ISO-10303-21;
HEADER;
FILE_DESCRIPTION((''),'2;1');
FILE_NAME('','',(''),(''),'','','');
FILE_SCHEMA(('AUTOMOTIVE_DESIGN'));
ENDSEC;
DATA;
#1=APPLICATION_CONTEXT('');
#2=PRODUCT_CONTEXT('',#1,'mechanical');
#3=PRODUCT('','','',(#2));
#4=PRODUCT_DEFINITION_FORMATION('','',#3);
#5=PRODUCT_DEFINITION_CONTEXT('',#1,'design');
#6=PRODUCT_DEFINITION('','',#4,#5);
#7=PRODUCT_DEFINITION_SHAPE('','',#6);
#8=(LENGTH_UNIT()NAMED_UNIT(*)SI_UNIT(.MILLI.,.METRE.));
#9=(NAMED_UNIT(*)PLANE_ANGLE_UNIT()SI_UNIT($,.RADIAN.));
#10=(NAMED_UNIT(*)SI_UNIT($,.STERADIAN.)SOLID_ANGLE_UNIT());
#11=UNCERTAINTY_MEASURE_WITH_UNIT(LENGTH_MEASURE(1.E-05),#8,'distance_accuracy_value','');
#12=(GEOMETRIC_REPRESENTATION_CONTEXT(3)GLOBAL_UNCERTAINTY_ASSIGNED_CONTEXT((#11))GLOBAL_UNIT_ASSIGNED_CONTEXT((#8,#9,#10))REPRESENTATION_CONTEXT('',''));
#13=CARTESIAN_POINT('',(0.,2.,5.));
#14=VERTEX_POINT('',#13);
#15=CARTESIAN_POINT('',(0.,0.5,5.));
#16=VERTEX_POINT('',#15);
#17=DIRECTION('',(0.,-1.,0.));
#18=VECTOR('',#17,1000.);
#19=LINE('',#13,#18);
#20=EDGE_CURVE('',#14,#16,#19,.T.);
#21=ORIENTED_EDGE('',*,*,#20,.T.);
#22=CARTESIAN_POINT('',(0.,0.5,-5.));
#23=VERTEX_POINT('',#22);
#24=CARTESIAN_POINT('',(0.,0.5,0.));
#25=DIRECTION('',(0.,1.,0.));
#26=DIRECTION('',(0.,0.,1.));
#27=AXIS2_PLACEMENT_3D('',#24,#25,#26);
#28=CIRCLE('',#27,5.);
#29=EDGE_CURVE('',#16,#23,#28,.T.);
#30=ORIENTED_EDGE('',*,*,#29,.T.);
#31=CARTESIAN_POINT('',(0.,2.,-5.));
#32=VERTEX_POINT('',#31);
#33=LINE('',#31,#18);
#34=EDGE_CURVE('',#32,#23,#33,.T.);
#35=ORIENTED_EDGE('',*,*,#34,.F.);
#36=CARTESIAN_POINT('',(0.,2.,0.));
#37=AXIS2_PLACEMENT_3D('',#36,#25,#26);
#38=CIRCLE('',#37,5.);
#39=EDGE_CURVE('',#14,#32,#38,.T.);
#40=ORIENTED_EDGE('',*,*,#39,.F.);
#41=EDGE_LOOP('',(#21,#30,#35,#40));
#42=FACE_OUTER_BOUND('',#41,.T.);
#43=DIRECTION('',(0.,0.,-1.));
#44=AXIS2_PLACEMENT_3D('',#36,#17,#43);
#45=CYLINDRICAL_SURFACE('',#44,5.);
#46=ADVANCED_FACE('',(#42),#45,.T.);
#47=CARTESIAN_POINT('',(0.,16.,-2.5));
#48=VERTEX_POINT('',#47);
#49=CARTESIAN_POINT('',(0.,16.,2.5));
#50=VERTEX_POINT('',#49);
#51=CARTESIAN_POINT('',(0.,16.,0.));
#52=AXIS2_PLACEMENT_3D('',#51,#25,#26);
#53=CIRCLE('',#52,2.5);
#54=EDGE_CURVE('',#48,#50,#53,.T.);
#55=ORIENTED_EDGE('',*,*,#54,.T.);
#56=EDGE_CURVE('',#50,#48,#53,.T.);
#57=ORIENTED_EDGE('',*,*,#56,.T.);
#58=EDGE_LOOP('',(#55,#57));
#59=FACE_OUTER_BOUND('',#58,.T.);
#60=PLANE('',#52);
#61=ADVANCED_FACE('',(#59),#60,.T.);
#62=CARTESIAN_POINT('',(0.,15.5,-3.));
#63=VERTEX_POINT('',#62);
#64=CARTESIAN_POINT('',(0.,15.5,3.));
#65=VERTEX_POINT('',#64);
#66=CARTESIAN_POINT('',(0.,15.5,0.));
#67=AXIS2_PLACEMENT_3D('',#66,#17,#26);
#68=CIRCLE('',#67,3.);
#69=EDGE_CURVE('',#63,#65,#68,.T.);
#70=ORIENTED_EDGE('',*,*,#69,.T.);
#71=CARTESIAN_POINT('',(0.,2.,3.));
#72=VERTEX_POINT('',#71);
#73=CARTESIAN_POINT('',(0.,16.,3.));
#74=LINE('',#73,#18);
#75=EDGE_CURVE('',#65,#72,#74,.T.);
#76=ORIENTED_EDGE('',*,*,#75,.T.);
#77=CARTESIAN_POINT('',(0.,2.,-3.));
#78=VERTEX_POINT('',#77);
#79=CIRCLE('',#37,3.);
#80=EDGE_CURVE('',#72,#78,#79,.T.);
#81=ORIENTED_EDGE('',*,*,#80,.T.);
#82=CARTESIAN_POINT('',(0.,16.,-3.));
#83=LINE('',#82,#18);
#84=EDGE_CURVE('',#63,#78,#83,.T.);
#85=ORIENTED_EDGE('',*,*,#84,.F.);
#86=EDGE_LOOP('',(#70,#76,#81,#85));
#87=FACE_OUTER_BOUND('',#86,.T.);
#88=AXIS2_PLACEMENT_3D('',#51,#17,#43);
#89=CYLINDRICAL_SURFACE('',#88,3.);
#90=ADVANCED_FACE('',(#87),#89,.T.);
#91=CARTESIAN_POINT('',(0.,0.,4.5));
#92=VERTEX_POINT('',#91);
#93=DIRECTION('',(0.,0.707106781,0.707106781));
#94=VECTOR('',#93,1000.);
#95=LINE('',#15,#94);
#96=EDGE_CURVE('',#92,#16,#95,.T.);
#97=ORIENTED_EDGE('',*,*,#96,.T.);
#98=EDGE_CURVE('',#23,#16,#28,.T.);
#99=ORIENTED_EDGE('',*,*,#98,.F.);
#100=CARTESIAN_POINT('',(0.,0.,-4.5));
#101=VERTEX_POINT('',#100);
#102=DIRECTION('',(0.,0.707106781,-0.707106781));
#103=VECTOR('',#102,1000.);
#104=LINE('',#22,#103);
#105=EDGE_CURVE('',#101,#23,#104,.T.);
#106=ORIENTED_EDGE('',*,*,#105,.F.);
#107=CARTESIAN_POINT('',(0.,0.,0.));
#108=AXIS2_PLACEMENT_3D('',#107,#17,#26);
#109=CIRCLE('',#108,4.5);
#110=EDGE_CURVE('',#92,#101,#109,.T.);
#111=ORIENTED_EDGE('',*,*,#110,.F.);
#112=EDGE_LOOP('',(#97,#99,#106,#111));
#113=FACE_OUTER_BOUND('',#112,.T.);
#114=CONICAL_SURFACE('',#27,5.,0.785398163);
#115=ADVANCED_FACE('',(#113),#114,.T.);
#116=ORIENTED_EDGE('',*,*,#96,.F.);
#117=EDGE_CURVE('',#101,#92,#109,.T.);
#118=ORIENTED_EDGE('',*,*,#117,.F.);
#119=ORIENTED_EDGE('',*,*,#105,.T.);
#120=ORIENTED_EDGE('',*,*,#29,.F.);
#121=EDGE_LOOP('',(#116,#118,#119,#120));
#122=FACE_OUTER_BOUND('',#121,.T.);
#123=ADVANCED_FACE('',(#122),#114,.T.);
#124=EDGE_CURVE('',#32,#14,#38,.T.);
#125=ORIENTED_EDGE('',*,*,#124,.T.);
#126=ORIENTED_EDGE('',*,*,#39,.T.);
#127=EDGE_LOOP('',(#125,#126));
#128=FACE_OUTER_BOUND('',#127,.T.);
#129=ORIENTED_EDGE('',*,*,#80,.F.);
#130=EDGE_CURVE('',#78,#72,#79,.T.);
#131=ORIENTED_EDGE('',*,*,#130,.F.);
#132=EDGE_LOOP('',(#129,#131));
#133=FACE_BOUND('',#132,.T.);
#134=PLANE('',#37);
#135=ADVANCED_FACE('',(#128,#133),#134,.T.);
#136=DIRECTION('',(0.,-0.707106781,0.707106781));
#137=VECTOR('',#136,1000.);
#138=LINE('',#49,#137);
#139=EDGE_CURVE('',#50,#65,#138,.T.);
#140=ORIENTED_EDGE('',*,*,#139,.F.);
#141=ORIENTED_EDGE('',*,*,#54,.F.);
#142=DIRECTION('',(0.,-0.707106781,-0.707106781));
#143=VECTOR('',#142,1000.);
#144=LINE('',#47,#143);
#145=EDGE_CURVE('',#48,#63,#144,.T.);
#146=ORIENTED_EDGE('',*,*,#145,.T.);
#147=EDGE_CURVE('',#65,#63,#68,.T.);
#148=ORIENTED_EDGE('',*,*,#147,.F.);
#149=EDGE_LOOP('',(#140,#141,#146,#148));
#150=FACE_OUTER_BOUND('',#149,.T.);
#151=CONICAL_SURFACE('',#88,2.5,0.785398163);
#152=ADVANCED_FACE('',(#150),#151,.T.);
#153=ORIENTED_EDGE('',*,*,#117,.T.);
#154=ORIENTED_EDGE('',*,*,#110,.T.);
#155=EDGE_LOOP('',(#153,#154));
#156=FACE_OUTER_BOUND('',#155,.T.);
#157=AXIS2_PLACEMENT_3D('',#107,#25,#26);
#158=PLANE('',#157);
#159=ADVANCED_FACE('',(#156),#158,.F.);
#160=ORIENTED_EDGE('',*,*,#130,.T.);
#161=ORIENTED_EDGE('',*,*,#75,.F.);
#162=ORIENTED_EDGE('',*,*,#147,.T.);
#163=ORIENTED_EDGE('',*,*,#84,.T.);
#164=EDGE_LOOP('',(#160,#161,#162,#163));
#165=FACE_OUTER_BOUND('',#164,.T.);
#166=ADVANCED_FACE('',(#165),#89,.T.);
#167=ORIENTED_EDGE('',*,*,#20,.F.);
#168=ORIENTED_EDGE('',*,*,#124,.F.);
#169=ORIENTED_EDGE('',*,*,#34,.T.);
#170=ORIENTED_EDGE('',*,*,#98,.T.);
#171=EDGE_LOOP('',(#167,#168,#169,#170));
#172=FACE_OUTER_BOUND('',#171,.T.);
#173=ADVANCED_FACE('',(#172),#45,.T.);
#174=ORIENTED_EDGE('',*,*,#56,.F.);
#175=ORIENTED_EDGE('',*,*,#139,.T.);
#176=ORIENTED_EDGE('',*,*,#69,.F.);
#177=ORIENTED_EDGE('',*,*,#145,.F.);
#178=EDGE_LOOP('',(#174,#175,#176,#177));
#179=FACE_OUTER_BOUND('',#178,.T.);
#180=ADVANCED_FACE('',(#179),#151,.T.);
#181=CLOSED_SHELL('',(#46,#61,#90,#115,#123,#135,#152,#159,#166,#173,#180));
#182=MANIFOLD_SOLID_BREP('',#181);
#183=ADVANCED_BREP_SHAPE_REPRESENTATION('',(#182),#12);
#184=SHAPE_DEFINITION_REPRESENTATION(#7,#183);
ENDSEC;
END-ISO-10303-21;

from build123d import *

# Parameters (mm, degrees)
SKETCH1_R           = 5
BOSS_EXTRUDE1_DEPTH = 2
SKETCH2_R           = 3
BOSS_EXTRUDE2_DEPTH = 14
CHAMFER1_SIZE       = 0.5


with BuildPart() as part:
    # Sketch1 → Boss-Extrude1 (new body)
    with BuildSketch(Plane(origin=(0, 0, 0), x_dir=(1, 0, 0), z_dir=(0, 1, 0))):
        with Locations(Location((0, 0, 0), (0, 0, 270))):
            Circle(SKETCH1_R)
    extrude(amount=BOSS_EXTRUDE1_DEPTH)

    # Sketch2 → Boss-Extrude2 (add)
    with BuildSketch(Plane(origin=(0, 2, 0), x_dir=(1, 0, 0), z_dir=(0, 1, 0))):
        with Locations(Location((0, 0, 0), (0, 0, 270))):
            Circle(SKETCH2_R)
    extrude(amount=BOSS_EXTRUDE2_DEPTH)

    # Chamfer1
    chamfer1_edges = [part.edges().sort_by_distance(p)[0] for p in [
        (0, 0, -5),
        (0, 16, -3),
    ]]
    chamfer(chamfer1_edges, length=CHAMFER1_SIZE)


solid = part.part
